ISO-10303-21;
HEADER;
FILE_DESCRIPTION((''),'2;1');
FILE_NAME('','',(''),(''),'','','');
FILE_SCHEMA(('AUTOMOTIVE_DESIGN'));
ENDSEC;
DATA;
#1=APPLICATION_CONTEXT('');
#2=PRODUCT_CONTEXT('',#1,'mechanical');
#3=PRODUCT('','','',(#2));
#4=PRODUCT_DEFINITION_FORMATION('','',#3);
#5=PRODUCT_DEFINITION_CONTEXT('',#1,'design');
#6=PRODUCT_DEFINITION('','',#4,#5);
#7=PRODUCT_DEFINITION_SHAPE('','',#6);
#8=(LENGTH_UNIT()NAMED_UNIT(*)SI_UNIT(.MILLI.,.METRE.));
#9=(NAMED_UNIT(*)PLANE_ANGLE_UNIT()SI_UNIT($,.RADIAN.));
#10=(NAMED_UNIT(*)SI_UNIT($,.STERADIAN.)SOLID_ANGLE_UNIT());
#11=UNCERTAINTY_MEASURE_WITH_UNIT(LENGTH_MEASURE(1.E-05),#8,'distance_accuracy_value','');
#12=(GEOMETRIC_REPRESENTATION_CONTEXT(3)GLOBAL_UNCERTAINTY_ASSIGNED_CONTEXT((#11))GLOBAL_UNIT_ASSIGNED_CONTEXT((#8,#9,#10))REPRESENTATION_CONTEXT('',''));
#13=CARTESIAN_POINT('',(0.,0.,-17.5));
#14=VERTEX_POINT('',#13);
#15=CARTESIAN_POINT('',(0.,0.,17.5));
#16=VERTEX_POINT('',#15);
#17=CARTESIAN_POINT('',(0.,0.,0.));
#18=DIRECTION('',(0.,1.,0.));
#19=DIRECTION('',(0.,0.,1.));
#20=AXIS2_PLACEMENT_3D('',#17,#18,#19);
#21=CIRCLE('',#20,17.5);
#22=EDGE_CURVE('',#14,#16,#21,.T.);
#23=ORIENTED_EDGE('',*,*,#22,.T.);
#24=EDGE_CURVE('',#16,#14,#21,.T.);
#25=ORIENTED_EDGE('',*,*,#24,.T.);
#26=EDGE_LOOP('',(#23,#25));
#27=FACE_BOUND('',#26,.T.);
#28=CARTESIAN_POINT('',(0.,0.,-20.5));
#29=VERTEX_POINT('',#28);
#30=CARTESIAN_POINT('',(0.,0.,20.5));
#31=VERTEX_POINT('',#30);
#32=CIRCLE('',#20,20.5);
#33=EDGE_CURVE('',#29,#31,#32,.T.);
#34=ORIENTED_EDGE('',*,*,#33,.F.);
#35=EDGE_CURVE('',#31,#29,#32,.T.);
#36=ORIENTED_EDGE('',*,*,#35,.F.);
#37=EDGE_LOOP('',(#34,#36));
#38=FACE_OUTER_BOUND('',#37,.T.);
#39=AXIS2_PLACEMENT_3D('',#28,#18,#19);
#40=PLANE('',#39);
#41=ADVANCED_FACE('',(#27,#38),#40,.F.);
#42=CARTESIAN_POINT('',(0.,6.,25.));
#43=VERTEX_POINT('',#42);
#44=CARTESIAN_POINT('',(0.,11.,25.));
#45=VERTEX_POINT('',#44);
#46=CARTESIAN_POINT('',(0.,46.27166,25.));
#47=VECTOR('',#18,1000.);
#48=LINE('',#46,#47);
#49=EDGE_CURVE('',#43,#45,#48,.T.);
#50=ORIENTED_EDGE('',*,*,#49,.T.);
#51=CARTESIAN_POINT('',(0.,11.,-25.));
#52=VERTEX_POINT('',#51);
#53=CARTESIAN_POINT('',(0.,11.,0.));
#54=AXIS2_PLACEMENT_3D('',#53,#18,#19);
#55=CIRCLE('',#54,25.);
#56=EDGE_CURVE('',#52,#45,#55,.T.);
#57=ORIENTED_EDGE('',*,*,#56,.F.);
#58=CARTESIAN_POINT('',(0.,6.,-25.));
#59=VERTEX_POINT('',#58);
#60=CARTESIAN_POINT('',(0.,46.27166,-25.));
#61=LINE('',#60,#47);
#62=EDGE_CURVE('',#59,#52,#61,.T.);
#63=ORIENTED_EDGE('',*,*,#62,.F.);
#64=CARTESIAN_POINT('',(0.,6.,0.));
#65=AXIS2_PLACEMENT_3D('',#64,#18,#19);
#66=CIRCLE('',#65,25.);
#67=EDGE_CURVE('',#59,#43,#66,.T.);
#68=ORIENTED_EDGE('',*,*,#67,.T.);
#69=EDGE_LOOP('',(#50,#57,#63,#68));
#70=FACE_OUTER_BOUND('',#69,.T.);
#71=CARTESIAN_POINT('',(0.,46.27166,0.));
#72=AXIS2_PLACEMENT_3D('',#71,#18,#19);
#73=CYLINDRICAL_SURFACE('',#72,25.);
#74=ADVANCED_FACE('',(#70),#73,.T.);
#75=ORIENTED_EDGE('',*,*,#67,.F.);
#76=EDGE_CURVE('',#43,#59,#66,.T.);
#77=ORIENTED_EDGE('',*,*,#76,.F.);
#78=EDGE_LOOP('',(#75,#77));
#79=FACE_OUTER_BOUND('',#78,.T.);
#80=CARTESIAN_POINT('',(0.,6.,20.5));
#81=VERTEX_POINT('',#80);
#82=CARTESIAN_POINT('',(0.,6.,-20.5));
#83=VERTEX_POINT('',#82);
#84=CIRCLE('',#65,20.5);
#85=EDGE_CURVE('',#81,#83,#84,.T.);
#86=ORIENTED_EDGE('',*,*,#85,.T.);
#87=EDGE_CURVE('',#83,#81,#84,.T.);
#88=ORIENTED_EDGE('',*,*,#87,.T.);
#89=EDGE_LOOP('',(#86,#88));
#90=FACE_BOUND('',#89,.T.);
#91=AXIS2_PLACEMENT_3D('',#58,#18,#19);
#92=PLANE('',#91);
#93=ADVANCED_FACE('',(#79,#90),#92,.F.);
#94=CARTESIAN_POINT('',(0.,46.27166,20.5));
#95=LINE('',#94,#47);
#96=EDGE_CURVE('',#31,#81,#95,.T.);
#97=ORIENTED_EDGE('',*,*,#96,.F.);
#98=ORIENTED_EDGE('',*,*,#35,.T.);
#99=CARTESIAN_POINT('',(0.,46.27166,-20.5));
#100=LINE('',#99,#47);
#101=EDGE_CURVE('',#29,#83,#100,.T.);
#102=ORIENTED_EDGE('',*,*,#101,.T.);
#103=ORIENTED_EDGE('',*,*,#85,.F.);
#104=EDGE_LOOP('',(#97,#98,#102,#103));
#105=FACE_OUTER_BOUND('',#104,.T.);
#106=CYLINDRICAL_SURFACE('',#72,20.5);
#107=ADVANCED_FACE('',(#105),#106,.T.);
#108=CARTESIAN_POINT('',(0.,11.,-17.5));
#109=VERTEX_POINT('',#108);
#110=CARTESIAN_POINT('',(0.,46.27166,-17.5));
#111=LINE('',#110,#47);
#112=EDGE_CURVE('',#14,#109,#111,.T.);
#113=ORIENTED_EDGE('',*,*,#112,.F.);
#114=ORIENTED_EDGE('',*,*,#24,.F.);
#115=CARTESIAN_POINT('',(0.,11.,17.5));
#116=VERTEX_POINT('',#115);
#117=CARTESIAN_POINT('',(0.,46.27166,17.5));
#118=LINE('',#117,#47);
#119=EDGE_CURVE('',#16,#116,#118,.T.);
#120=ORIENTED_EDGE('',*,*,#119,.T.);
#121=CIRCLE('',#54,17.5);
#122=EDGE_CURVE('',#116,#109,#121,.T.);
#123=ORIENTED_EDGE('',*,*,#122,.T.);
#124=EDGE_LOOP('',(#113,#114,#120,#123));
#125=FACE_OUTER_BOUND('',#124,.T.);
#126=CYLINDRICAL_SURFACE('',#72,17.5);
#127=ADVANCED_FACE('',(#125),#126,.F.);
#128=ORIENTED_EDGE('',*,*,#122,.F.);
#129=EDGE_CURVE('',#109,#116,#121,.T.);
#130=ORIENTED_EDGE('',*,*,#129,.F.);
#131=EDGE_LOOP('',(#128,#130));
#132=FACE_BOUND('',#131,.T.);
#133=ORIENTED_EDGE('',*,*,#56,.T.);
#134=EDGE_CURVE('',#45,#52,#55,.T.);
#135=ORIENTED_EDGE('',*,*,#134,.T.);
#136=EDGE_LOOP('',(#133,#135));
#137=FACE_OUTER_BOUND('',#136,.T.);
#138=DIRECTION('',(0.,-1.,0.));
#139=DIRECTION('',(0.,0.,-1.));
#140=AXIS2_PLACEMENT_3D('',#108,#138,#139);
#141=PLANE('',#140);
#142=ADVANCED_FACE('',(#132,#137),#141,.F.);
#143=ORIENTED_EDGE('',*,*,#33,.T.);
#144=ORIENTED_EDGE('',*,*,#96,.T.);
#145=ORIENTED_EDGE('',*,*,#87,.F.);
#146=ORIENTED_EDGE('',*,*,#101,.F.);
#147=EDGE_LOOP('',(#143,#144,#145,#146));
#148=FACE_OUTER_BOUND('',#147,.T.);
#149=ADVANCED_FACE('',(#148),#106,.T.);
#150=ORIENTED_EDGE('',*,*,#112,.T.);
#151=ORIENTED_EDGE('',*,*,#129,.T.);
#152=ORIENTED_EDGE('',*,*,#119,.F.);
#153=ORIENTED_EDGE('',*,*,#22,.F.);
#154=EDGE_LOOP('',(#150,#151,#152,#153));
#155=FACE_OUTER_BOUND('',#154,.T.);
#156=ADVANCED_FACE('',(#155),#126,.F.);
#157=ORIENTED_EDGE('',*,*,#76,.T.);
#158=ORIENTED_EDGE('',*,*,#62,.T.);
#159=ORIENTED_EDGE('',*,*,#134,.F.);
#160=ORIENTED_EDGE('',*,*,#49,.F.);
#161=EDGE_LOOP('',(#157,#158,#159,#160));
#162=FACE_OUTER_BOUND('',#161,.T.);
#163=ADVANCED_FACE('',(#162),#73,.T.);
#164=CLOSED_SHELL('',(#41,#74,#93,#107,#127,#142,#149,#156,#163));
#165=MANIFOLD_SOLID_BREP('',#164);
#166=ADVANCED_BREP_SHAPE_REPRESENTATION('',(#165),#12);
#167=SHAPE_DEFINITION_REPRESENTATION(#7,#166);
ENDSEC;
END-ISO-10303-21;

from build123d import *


with BuildPart() as part:
    # 草图1 → 旋转1 (revolve)
    with BuildSketch(Plane(origin=(0, 0, 0), x_dir=(0, 0, -1), z_dir=(1, 0, 0)), mode=Mode.PRIVATE) as revolve_1_sk:
        Polygon((17.5, 0), (17.5, 11), (25, 11), (25, 6), (20.5, 6), (20.5, 0), align=None)
    revolve(revolve_1_sk.sketch.rotate(Axis((0, 46.271659978, 0), (0, -1, 0)), 180), axis=Axis((0, 46.271659978, 0), (0, -1, 0)))


solid = part.part
